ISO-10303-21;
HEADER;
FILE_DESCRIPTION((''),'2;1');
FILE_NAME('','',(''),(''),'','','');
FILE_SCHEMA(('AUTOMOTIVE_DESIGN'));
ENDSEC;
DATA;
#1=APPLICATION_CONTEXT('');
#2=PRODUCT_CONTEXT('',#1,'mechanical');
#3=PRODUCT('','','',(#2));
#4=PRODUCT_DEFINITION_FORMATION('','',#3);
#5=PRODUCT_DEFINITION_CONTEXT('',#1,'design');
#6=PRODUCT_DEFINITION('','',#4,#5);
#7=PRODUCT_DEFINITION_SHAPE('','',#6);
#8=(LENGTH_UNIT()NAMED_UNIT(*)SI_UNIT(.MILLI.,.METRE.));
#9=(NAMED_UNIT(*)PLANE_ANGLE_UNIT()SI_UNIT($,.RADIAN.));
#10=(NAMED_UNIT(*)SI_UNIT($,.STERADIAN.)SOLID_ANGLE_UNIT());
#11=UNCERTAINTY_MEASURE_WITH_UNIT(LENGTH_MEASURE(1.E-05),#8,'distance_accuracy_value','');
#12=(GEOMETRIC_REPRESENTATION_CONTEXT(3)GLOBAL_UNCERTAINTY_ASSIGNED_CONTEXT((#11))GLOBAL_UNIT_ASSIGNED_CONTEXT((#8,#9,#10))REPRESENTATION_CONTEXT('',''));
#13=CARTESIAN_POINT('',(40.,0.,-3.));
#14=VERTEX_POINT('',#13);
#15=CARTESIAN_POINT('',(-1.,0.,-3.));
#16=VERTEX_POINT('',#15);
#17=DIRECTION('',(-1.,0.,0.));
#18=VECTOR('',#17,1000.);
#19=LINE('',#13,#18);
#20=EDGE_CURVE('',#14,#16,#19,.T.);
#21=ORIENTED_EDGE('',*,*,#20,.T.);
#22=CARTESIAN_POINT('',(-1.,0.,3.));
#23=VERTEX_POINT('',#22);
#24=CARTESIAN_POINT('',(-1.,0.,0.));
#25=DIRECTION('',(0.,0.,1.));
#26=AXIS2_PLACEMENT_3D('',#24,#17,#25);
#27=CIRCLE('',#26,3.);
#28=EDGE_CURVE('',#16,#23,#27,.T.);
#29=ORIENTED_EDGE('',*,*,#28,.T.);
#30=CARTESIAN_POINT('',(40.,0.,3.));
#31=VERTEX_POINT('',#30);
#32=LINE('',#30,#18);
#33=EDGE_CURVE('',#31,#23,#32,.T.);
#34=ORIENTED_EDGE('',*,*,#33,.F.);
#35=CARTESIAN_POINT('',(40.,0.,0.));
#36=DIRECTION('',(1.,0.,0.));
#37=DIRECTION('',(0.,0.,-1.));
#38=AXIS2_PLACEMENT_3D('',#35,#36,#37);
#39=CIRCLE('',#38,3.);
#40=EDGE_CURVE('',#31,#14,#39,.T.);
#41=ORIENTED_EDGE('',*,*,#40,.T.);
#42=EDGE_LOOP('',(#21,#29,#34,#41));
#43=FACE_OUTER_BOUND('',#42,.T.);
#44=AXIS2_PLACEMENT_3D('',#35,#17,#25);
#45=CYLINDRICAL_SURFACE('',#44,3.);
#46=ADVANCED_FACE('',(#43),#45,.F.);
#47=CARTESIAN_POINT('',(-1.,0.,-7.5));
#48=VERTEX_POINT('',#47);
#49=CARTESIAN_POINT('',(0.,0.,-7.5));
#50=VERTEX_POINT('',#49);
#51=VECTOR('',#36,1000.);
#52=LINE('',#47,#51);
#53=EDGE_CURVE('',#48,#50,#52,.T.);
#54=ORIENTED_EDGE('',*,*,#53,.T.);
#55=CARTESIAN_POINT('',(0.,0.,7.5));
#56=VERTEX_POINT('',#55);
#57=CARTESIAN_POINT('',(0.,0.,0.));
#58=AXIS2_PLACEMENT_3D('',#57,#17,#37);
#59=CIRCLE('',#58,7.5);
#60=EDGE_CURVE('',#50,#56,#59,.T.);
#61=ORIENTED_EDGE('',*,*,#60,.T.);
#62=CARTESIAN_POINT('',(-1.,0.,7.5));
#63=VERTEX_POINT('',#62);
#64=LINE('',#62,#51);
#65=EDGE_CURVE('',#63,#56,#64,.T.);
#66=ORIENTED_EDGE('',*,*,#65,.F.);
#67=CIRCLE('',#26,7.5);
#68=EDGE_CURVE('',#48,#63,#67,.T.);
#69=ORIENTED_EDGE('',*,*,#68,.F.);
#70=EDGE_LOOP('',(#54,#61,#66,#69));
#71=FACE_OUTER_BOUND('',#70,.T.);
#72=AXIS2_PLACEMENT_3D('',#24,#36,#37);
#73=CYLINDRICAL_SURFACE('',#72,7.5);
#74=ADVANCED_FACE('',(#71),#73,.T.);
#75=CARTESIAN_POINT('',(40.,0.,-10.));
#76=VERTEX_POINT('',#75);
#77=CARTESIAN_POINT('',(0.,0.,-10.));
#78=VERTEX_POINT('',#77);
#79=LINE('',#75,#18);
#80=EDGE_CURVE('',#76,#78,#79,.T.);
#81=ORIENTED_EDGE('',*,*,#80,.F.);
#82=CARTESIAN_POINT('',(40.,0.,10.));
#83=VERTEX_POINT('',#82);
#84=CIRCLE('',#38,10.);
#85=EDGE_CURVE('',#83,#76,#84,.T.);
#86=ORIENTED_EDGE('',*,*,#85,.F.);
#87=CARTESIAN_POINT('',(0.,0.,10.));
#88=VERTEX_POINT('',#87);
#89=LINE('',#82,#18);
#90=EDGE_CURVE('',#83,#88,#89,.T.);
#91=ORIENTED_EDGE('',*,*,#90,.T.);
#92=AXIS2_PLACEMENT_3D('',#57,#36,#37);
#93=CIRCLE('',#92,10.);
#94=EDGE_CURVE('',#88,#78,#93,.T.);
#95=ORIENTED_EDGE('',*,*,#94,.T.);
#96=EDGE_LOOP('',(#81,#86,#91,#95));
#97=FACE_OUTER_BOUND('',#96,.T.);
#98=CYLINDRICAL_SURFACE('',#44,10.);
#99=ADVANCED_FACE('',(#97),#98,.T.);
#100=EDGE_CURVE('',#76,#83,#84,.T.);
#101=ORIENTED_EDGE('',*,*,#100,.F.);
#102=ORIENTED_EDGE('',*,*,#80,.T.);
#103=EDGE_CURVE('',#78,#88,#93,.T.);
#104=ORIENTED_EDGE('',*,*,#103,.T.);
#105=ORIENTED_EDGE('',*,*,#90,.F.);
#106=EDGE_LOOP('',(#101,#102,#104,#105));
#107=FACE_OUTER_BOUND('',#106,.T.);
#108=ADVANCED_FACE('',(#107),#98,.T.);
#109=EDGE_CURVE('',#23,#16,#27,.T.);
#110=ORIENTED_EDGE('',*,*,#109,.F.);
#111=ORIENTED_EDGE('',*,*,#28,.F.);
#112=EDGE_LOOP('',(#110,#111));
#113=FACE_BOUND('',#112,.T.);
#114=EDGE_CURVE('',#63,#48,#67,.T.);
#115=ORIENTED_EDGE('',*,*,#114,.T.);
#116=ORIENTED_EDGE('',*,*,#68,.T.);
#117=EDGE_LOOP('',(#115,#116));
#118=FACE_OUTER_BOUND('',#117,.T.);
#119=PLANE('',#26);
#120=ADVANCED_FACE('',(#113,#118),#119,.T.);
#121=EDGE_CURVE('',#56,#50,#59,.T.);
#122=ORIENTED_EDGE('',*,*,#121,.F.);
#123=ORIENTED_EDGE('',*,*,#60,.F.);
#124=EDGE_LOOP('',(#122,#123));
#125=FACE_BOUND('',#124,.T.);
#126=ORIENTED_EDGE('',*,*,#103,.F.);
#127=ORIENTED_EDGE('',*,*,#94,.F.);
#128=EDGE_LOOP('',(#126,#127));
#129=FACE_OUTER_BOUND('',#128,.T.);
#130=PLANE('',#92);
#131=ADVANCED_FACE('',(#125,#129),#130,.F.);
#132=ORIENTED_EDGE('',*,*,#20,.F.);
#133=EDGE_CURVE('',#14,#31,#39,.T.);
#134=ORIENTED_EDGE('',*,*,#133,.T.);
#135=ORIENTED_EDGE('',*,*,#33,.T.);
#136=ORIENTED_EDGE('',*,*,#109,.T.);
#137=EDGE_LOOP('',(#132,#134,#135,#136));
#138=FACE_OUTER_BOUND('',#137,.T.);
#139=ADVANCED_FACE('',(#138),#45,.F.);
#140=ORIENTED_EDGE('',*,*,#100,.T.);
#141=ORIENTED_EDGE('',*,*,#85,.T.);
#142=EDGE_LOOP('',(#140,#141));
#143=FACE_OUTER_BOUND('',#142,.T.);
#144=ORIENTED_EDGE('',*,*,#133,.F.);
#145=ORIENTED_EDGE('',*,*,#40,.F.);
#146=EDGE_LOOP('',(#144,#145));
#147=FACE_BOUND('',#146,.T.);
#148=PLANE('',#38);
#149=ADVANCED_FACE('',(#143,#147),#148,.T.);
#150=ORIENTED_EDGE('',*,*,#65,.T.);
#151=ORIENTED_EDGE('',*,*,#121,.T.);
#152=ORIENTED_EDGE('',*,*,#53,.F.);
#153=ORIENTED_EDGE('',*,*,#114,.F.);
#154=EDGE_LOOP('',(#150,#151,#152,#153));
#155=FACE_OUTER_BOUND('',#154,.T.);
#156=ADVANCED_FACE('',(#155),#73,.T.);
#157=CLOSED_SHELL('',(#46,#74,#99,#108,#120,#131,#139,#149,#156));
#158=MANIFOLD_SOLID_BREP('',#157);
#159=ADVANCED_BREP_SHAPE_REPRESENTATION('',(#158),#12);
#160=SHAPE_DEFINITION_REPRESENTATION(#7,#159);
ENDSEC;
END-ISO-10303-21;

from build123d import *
from build123d.topology import SkipClean

# Parameters (mm, degrees)
SKETCH_1_R      = 10
SKETCH_1_R_2    = 3
EXTRUDE_1_DEPTH = 40
EXTRUDE_START   = 1
SKETCH_3_R      = 7.5
SKETCH_3_R_2    = 3
EXTRUDE_2_DEPTH = 1


with BuildPart() as part:
    # 草图1 → 凸台-拉伸1 (new body)
    with BuildSketch(Plane(origin=(0, 0, 0), x_dir=(0, 0, -1), z_dir=(1, 0, 0))):
        Circle(SKETCH_1_R)
        Circle(SKETCH_1_R_2, mode=Mode.SUBTRACT)
    extrude(amount=EXTRUDE_1_DEPTH)

    # 草图3 → 凸台-拉伸2 (add)
    with SkipClean():  # the faces are left unmerged after this step: merging them gives an invalid solid
        with BuildSketch(Plane.ZY.offset(EXTRUDE_START)):
            with Locations(Location((0, 0, 0), (0, 0, 180))):
                Circle(SKETCH_3_R)
            Circle(SKETCH_3_R_2, mode=Mode.SUBTRACT)
        extrude(amount=-EXTRUDE_2_DEPTH)


solid = part.part
